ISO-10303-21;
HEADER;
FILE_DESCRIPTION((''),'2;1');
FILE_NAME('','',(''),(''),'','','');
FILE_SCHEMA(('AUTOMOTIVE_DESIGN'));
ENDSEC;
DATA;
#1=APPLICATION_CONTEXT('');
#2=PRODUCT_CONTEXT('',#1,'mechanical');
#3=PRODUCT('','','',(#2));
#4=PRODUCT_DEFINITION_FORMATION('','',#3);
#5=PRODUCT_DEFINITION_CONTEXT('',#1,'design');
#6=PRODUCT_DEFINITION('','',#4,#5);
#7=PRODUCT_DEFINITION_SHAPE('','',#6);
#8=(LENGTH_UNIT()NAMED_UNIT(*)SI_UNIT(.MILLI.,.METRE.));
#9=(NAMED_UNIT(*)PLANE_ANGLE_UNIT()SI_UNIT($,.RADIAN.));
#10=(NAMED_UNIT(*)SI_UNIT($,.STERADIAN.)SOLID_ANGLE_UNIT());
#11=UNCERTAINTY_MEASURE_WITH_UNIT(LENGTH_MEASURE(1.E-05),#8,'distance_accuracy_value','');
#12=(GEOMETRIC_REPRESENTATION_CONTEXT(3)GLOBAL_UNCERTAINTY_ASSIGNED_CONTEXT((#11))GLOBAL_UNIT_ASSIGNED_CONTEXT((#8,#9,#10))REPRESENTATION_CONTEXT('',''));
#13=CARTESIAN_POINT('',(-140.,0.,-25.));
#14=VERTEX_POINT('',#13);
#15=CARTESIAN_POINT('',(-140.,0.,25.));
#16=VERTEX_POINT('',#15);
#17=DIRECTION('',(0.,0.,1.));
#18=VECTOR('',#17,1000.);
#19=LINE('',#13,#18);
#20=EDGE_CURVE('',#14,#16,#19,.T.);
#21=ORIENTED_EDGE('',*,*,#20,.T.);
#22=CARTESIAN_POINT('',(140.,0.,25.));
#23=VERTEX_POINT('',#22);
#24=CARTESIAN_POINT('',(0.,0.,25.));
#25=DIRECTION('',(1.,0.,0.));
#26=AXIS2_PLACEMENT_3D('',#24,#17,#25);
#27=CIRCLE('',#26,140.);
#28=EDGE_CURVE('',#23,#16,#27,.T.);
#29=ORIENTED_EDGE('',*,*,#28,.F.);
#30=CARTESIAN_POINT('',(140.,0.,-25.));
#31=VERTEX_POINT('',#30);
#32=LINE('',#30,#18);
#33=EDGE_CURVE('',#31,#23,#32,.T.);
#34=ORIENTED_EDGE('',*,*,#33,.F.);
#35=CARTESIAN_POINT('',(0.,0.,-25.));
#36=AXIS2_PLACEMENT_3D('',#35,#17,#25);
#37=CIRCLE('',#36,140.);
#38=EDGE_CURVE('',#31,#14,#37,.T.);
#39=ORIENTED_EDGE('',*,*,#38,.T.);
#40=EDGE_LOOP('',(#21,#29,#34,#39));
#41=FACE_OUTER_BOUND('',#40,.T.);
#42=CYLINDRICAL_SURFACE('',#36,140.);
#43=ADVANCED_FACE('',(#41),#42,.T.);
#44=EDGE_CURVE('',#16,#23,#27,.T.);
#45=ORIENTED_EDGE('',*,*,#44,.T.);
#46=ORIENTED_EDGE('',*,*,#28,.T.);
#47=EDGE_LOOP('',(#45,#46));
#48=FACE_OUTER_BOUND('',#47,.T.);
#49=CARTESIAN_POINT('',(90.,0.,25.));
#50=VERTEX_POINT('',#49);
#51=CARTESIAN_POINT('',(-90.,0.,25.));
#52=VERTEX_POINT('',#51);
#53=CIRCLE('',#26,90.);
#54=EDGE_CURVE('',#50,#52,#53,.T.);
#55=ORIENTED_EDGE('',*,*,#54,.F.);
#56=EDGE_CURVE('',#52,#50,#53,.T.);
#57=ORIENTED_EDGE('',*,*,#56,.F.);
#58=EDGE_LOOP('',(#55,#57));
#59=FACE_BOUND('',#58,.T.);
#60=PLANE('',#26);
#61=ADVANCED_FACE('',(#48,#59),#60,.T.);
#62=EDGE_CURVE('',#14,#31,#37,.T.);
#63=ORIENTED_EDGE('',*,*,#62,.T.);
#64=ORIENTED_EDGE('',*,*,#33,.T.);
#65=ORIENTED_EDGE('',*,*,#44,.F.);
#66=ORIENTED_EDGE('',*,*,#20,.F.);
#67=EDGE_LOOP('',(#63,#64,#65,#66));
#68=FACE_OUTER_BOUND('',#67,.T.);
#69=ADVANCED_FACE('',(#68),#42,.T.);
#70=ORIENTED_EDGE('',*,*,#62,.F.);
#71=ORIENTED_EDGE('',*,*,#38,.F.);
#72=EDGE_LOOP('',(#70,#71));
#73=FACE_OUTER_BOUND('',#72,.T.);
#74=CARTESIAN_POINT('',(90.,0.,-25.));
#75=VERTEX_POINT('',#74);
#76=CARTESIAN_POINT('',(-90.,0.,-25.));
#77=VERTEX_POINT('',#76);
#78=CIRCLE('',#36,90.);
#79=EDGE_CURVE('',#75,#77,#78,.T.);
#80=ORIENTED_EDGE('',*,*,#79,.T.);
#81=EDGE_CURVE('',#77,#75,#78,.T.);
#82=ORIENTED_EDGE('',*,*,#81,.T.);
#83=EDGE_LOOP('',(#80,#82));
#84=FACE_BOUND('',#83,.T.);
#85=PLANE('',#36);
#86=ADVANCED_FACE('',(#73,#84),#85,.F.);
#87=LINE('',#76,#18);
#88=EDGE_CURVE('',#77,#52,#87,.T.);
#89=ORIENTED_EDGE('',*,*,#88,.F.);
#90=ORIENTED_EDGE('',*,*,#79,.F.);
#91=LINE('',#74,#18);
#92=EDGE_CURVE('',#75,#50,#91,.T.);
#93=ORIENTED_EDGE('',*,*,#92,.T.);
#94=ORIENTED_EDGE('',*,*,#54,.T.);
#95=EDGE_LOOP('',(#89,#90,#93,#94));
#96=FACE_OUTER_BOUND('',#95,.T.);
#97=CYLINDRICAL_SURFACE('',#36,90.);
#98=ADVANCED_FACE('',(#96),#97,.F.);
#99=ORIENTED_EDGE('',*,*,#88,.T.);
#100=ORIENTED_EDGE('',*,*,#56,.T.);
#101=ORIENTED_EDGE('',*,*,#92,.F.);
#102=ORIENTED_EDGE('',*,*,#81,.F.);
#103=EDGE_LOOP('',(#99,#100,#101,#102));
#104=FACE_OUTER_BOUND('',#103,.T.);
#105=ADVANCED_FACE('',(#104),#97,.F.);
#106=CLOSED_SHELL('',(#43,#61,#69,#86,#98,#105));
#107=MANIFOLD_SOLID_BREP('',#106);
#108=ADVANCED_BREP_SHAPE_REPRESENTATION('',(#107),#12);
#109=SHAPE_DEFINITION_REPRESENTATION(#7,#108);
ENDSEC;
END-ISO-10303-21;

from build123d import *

# Parameters (mm, degrees)
SKETCH_1_R      = 140
SKETCH_1_R_2    = 90
EXTRUDE_1_DEPTH = 25


with BuildPart() as part:
    # 草图1 → 凸台-拉伸1 (new, symmetric)
    with BuildSketch(Plane.XY):
        Circle(SKETCH_1_R)
        Circle(SKETCH_1_R_2, mode=Mode.SUBTRACT)
    extrude(amount=EXTRUDE_1_DEPTH, both=True)


solid = part.part
